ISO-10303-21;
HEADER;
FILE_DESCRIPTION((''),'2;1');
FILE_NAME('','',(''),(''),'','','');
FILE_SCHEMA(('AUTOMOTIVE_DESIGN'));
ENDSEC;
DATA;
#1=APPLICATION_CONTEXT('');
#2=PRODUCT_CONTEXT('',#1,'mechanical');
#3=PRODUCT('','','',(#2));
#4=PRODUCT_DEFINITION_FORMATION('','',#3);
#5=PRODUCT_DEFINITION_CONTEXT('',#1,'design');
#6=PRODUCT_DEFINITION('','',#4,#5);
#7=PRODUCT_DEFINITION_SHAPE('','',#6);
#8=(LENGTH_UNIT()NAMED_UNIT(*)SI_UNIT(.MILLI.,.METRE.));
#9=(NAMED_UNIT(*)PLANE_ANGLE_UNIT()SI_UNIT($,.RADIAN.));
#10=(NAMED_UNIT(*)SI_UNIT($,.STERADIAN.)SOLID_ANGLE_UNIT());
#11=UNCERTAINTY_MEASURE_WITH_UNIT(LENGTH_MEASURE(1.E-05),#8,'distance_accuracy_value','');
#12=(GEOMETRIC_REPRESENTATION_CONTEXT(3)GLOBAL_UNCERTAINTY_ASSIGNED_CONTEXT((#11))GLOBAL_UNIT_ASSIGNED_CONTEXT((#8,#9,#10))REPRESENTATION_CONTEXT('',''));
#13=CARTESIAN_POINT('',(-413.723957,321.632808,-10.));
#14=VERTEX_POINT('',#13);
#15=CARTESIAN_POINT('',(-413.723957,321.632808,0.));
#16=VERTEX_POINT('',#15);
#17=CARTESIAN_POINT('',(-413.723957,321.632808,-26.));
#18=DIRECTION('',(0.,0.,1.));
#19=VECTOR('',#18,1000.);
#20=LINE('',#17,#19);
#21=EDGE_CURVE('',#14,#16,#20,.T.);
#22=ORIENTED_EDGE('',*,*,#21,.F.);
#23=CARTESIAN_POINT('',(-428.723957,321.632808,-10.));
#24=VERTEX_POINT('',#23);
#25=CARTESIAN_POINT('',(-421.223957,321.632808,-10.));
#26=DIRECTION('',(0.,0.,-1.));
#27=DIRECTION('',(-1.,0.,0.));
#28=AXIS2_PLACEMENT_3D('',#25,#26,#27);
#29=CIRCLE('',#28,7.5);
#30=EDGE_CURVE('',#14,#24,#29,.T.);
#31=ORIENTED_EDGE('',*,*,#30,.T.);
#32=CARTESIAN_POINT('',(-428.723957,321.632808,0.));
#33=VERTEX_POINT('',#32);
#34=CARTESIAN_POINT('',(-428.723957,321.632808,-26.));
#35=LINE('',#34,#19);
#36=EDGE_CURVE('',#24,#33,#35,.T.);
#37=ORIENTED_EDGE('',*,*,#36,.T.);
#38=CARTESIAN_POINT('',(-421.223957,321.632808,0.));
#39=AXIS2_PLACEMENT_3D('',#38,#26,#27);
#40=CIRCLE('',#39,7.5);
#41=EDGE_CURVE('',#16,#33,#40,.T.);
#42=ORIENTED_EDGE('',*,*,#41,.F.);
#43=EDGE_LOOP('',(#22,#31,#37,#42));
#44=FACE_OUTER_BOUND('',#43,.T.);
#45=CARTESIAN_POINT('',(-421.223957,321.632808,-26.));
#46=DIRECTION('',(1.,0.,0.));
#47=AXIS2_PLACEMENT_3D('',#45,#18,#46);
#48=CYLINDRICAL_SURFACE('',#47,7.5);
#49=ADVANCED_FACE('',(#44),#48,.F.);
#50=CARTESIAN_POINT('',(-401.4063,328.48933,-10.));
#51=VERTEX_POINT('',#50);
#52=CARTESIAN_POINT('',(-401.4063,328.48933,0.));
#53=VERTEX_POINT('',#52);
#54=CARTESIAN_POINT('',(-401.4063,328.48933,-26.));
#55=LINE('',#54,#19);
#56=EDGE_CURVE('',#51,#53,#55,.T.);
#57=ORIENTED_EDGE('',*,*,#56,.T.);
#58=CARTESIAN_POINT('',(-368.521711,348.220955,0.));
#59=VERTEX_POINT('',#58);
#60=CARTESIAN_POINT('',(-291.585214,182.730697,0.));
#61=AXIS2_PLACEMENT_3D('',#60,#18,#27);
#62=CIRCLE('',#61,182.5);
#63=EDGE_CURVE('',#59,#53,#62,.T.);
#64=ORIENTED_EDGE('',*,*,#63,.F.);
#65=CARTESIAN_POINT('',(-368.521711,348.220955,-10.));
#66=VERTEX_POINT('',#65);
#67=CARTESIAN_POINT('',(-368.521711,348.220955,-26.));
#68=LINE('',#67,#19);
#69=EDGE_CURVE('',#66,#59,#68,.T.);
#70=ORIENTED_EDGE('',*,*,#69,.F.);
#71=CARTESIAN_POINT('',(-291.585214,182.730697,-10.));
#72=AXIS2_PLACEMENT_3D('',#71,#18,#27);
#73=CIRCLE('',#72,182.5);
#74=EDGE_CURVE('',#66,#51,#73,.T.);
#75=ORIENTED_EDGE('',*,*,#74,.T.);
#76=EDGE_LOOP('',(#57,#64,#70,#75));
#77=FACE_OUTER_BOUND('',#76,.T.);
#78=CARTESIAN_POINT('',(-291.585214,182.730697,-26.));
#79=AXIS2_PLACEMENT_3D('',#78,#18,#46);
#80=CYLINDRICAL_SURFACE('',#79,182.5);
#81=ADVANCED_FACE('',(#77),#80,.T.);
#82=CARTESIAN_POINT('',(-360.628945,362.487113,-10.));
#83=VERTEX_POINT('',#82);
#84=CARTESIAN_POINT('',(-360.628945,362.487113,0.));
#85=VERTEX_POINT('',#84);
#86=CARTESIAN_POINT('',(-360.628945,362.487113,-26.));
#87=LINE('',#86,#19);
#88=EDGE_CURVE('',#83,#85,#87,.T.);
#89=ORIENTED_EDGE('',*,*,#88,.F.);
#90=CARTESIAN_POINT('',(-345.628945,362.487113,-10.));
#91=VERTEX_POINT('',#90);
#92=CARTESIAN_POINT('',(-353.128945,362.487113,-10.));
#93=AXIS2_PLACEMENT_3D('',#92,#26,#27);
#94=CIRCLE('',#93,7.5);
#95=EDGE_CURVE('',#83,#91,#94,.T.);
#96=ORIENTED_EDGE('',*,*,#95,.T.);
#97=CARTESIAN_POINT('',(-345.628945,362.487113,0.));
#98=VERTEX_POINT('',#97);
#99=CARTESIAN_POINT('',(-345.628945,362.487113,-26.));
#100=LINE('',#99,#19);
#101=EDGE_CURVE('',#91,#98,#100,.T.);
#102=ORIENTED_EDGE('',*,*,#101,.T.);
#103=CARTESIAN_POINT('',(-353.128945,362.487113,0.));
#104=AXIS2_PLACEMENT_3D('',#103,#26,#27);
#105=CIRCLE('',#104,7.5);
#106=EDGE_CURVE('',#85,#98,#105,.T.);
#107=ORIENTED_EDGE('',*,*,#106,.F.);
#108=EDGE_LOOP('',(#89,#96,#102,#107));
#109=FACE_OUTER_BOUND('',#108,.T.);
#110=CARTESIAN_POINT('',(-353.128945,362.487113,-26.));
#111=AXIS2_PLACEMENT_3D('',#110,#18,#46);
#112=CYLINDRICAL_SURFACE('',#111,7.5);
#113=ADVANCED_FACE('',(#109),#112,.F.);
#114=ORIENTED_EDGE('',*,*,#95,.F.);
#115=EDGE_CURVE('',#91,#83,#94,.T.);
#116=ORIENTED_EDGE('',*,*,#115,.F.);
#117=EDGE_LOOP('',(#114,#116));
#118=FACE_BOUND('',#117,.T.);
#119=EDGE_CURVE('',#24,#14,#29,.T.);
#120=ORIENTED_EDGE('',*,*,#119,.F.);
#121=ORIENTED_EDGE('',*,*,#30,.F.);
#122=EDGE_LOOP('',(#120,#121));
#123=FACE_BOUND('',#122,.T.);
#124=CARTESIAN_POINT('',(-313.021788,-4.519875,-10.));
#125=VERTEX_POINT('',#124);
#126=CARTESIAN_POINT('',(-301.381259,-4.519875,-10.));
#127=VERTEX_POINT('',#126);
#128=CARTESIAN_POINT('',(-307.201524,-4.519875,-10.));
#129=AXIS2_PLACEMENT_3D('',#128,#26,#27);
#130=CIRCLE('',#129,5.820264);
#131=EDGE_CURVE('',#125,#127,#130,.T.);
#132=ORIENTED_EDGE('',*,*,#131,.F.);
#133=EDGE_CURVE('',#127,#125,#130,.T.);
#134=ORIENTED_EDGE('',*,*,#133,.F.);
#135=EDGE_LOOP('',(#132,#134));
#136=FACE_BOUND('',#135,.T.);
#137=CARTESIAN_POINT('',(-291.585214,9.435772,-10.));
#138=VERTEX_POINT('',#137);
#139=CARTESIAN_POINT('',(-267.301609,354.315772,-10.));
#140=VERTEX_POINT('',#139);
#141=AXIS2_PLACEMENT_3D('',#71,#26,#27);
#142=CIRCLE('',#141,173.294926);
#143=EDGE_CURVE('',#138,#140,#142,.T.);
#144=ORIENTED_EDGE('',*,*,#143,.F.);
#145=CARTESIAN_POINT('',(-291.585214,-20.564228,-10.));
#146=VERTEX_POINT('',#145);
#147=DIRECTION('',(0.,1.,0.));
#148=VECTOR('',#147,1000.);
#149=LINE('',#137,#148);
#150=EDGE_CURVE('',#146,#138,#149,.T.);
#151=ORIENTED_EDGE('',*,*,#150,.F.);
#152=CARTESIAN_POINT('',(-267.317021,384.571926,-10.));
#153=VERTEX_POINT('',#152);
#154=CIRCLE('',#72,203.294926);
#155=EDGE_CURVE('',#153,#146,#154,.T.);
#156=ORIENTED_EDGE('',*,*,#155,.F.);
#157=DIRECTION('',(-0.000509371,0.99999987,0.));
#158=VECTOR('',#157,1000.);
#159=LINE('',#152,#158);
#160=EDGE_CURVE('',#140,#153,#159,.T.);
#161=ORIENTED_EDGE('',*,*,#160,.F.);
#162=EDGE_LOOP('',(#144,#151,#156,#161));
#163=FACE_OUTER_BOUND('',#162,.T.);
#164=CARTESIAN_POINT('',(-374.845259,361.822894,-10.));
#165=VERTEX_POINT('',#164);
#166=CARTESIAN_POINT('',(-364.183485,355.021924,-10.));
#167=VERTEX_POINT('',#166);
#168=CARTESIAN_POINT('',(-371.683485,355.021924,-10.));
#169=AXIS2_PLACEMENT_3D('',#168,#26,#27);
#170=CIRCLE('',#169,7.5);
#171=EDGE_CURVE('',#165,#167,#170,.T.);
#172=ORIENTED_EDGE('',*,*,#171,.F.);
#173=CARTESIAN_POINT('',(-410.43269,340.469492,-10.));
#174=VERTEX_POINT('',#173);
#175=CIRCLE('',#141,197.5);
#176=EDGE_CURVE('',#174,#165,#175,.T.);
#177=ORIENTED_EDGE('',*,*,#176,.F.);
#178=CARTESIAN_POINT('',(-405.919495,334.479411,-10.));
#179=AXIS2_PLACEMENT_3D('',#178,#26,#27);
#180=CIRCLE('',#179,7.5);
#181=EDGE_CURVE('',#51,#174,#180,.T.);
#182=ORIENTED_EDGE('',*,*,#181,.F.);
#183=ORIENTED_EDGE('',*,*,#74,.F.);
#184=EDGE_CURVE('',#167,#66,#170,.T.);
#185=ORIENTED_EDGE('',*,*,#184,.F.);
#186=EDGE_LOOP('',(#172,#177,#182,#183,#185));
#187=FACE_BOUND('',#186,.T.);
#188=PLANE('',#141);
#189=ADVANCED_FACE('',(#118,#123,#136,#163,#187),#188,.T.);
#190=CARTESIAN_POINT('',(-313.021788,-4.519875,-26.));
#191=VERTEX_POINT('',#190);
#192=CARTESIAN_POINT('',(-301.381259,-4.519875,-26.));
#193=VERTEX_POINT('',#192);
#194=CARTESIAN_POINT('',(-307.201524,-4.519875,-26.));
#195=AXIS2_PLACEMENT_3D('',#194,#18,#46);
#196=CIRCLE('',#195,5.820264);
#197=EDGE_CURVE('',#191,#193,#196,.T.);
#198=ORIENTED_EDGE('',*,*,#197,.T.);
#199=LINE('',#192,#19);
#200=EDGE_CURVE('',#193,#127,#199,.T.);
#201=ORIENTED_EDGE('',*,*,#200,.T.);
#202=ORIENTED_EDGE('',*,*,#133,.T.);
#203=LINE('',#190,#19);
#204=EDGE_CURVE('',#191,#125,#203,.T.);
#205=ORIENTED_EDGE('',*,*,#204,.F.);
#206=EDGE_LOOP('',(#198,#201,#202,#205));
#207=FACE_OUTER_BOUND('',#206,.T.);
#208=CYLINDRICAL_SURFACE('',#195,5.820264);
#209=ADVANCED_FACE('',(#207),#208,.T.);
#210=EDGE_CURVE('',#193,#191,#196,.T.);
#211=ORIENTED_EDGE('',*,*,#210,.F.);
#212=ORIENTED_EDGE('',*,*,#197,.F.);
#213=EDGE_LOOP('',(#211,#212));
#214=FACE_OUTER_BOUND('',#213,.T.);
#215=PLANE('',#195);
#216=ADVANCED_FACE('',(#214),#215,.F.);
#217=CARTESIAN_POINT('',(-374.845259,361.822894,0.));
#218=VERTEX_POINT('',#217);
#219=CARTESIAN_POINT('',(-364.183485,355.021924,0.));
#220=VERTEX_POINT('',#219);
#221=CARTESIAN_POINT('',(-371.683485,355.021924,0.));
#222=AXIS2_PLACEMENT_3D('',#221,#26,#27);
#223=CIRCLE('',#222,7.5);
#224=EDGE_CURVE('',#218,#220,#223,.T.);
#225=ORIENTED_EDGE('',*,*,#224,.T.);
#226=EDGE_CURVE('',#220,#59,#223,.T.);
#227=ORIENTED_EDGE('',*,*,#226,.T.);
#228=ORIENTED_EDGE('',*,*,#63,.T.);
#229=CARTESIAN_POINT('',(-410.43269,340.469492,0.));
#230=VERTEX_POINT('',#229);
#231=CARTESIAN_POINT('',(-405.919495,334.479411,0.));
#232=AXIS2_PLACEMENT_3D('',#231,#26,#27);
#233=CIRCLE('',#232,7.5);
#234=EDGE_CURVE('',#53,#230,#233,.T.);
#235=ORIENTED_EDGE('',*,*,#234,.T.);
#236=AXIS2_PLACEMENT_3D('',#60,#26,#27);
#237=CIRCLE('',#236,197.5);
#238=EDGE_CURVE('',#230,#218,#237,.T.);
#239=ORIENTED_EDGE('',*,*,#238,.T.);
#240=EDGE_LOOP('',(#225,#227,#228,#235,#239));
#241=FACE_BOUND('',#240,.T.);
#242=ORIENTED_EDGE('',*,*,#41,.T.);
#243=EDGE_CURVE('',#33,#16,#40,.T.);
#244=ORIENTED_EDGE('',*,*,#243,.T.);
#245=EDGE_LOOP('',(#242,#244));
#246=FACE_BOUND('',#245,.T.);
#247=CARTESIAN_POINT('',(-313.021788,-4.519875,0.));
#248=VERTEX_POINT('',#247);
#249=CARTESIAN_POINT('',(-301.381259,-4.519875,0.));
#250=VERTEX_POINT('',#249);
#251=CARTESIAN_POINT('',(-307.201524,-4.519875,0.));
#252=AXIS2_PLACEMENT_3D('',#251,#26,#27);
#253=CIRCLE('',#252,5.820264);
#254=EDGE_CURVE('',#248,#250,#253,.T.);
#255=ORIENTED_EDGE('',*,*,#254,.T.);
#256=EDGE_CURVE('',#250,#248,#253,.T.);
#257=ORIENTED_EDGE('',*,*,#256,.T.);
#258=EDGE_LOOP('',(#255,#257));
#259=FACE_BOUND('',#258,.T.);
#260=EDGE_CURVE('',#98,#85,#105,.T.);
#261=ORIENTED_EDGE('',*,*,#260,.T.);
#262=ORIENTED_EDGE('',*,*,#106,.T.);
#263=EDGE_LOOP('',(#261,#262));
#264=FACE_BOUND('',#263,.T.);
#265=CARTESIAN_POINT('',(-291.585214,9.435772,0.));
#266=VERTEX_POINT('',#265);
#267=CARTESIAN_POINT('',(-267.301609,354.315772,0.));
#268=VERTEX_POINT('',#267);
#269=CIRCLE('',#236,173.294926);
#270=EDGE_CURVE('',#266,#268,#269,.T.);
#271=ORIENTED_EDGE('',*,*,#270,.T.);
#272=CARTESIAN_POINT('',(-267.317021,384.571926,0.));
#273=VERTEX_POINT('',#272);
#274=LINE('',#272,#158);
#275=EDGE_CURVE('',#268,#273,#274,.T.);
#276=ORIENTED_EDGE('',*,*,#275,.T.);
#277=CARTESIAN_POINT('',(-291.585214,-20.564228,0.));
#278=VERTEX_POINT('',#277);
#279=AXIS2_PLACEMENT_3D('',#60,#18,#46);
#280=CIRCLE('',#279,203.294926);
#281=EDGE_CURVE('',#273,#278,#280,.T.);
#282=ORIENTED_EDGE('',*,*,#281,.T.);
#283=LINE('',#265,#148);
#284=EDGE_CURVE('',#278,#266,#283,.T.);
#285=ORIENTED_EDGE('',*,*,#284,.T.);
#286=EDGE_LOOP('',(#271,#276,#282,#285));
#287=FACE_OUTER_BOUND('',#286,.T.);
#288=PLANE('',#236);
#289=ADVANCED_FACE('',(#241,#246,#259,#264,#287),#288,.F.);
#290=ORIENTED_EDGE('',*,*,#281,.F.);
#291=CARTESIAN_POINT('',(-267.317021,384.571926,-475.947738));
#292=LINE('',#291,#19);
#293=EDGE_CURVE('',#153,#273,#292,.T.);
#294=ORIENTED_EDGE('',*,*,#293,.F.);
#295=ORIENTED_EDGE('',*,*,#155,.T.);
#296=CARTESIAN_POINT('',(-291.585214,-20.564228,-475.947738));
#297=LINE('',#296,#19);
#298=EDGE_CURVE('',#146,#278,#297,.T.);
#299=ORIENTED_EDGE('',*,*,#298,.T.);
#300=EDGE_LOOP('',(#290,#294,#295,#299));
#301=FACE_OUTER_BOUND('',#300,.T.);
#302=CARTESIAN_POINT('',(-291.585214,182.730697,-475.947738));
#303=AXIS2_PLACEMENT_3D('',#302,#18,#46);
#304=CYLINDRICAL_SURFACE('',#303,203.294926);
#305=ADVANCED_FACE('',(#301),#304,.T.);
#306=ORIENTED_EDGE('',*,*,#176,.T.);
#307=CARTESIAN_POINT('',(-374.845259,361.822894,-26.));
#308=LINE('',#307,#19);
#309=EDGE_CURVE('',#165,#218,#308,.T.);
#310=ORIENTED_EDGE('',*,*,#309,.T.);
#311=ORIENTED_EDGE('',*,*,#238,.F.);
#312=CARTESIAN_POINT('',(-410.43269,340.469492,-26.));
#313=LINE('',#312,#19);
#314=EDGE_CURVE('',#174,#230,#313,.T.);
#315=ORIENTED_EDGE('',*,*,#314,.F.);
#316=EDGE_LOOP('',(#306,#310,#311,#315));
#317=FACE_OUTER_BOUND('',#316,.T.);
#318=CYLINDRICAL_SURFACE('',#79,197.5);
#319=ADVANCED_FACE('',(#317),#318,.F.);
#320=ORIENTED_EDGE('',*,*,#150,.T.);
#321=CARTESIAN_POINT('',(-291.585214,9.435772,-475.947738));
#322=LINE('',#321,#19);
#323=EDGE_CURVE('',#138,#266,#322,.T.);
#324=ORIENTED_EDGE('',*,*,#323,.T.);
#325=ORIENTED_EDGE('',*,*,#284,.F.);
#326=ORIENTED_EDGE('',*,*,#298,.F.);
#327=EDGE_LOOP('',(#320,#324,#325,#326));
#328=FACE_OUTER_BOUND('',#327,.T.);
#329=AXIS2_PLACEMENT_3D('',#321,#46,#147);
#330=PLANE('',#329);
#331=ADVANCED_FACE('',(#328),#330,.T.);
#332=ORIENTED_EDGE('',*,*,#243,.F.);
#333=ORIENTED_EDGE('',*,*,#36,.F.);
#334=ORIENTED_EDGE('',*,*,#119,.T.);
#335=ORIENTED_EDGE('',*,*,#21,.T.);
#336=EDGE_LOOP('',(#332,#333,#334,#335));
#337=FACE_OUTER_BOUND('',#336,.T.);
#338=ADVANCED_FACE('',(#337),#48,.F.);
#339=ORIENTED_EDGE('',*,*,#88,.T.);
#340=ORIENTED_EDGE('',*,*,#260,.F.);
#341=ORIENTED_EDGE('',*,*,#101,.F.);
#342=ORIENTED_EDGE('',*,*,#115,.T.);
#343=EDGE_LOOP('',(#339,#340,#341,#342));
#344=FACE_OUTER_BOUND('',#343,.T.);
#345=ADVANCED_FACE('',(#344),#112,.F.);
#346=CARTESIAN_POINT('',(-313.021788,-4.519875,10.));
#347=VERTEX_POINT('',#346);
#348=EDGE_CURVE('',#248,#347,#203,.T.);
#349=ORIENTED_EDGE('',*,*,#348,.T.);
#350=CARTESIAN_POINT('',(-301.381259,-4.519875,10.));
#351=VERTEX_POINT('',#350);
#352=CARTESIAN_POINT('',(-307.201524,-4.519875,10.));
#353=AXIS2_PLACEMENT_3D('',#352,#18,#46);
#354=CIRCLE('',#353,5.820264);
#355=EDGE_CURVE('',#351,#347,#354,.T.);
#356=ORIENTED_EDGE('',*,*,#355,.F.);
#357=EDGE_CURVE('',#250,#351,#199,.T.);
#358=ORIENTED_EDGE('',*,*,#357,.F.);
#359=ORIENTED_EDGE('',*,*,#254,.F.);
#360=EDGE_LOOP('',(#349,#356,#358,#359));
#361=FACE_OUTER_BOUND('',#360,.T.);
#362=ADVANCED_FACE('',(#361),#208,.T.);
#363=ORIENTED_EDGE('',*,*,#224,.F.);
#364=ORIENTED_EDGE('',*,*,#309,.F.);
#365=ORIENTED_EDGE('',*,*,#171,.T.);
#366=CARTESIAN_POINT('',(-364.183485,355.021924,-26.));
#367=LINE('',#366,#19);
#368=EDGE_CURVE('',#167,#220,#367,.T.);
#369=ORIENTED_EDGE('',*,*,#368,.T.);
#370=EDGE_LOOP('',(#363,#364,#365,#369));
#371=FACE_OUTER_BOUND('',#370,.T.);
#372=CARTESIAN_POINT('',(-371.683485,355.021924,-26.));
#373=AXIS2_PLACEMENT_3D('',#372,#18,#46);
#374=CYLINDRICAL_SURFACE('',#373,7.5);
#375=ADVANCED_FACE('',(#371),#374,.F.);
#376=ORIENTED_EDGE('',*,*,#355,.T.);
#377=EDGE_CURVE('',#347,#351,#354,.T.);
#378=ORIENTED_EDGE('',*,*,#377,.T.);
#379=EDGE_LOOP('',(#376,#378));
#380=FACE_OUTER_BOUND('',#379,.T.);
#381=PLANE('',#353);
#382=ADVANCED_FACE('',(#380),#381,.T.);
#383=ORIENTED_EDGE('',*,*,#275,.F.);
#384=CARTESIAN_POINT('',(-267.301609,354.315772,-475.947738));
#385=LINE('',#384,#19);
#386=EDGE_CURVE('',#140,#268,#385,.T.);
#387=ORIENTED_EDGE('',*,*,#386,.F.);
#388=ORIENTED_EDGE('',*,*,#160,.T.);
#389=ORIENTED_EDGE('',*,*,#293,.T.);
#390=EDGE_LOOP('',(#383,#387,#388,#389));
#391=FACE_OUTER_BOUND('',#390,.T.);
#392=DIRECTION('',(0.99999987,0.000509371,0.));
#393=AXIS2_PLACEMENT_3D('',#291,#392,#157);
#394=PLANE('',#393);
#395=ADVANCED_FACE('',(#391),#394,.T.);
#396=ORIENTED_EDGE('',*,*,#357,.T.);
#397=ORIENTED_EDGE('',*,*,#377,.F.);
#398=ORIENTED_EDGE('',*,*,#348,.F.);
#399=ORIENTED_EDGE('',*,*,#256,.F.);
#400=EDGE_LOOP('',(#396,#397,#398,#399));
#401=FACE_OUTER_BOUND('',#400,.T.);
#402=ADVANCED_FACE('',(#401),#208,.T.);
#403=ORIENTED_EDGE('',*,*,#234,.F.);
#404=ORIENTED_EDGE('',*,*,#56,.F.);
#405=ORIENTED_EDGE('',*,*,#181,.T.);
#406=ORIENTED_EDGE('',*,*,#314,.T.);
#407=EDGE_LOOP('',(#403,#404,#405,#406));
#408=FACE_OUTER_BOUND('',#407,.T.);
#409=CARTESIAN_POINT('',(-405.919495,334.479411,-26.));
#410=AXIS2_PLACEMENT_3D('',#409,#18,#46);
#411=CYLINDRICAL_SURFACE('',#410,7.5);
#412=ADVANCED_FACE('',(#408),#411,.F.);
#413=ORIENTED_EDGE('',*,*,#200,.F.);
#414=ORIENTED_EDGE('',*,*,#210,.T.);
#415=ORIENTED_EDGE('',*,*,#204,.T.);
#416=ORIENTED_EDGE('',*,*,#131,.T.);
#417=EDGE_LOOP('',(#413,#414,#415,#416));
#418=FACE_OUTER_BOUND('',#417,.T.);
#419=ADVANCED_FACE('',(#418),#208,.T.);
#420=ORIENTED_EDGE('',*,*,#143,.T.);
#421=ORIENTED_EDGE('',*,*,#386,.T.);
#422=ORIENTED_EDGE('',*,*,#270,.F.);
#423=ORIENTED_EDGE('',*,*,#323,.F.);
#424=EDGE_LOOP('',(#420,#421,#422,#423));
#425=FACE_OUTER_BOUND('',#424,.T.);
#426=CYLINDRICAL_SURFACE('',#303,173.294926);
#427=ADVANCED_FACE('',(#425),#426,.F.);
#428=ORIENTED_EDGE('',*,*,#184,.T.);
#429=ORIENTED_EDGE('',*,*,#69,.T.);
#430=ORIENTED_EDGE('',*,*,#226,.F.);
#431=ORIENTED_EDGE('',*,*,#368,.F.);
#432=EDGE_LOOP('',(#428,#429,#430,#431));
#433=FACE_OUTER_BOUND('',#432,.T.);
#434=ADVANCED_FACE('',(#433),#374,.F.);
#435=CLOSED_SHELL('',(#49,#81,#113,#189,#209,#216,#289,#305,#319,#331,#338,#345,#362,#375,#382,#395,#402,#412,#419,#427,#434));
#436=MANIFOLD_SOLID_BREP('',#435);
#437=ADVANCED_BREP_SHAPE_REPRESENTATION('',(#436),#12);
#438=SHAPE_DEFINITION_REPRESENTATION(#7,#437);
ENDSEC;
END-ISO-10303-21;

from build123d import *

# Parameters (mm, degrees)
BOSS_EXTRUDE1_DEPTH      = 10
BOSS_EXTRUDE2_DEPTH      = 10
BOSS_EXTRUDE2_DEPTH_BACK = 26
SKETCH2_R                = 5.820264096
CUT_EXTRUDE1_DEPTH       = 629.17046577
CUT_EXTRUDE1_DEPTH_BACK  = 629.17046577
SKETCH3_R                = 7.5


with BuildPart() as part:
    # Sketch1 → Boss-Extrude1 (new body)
    with BuildSketch(Plane.XY):
        with BuildLine():
            Line((-267.317020812, 384.57192575), (-267.301609192, 354.315771574))
            ThreePointArc((-267.301609192, 354.315771574), (-464.45214838, 194.902560898), (-291.585214163, 9.435771703))
            Line((-291.585214163, 9.435771703), (-291.585214163, -20.564228297))
            ThreePointArc((-291.585214163, -20.564228297), (-494.516390011, 194.886544), (-267.317020812, 384.57192575))
        make_face()
    extrude(amount=-BOSS_EXTRUDE1_DEPTH)

    # Sketch2 → Boss-Extrude2 (add, two sides: drawn at the far end of the back side and taken through both)
    with BuildSketch(Plane.XY.offset(-BOSS_EXTRUDE2_DEPTH_BACK)):
        with Locations((-307.201523558, -4.519874966)):
            Circle(SKETCH2_R)
    extrude(amount=BOSS_EXTRUDE2_DEPTH + BOSS_EXTRUDE2_DEPTH_BACK)

    # Sketch3 → Cut-Extrude1 (cut, two sides: drawn at the far end of the back side and taken through both)
    with BuildSketch(Plane.XY.offset(-CUT_EXTRUDE1_DEPTH_BACK)):
        with Locations(Location((-421.223956701, 321.632808197, 0), (0, 0, 180))):
            Circle(SKETCH3_R)
        with Locations(Location((-353.128945359, 362.487113382, 0), (0, 0, 180))):
            Circle(SKETCH3_R)
        with BuildLine():
            ThreePointArc((-374.845259184, 361.822893879), (-393.201425865, 352.083570004), (-410.432690408, 340.469492039))
            ThreePointArc((-410.432690408, 340.469492039), (-411.909575924, 329.966215923), (-401.406299807, 328.489330407))
            ThreePointArc((-401.406299807, 328.489330407), (-385.4837389, 339.221326502), (-368.521711461, 348.220954892))
            ThreePointArc((-368.521711461, 348.220954892), (-364.882515829, 358.183698247), (-374.845259184, 361.822893879))
        make_face()
    extrude(amount=CUT_EXTRUDE1_DEPTH + CUT_EXTRUDE1_DEPTH_BACK, mode=Mode.SUBTRACT)


solid = part.part
